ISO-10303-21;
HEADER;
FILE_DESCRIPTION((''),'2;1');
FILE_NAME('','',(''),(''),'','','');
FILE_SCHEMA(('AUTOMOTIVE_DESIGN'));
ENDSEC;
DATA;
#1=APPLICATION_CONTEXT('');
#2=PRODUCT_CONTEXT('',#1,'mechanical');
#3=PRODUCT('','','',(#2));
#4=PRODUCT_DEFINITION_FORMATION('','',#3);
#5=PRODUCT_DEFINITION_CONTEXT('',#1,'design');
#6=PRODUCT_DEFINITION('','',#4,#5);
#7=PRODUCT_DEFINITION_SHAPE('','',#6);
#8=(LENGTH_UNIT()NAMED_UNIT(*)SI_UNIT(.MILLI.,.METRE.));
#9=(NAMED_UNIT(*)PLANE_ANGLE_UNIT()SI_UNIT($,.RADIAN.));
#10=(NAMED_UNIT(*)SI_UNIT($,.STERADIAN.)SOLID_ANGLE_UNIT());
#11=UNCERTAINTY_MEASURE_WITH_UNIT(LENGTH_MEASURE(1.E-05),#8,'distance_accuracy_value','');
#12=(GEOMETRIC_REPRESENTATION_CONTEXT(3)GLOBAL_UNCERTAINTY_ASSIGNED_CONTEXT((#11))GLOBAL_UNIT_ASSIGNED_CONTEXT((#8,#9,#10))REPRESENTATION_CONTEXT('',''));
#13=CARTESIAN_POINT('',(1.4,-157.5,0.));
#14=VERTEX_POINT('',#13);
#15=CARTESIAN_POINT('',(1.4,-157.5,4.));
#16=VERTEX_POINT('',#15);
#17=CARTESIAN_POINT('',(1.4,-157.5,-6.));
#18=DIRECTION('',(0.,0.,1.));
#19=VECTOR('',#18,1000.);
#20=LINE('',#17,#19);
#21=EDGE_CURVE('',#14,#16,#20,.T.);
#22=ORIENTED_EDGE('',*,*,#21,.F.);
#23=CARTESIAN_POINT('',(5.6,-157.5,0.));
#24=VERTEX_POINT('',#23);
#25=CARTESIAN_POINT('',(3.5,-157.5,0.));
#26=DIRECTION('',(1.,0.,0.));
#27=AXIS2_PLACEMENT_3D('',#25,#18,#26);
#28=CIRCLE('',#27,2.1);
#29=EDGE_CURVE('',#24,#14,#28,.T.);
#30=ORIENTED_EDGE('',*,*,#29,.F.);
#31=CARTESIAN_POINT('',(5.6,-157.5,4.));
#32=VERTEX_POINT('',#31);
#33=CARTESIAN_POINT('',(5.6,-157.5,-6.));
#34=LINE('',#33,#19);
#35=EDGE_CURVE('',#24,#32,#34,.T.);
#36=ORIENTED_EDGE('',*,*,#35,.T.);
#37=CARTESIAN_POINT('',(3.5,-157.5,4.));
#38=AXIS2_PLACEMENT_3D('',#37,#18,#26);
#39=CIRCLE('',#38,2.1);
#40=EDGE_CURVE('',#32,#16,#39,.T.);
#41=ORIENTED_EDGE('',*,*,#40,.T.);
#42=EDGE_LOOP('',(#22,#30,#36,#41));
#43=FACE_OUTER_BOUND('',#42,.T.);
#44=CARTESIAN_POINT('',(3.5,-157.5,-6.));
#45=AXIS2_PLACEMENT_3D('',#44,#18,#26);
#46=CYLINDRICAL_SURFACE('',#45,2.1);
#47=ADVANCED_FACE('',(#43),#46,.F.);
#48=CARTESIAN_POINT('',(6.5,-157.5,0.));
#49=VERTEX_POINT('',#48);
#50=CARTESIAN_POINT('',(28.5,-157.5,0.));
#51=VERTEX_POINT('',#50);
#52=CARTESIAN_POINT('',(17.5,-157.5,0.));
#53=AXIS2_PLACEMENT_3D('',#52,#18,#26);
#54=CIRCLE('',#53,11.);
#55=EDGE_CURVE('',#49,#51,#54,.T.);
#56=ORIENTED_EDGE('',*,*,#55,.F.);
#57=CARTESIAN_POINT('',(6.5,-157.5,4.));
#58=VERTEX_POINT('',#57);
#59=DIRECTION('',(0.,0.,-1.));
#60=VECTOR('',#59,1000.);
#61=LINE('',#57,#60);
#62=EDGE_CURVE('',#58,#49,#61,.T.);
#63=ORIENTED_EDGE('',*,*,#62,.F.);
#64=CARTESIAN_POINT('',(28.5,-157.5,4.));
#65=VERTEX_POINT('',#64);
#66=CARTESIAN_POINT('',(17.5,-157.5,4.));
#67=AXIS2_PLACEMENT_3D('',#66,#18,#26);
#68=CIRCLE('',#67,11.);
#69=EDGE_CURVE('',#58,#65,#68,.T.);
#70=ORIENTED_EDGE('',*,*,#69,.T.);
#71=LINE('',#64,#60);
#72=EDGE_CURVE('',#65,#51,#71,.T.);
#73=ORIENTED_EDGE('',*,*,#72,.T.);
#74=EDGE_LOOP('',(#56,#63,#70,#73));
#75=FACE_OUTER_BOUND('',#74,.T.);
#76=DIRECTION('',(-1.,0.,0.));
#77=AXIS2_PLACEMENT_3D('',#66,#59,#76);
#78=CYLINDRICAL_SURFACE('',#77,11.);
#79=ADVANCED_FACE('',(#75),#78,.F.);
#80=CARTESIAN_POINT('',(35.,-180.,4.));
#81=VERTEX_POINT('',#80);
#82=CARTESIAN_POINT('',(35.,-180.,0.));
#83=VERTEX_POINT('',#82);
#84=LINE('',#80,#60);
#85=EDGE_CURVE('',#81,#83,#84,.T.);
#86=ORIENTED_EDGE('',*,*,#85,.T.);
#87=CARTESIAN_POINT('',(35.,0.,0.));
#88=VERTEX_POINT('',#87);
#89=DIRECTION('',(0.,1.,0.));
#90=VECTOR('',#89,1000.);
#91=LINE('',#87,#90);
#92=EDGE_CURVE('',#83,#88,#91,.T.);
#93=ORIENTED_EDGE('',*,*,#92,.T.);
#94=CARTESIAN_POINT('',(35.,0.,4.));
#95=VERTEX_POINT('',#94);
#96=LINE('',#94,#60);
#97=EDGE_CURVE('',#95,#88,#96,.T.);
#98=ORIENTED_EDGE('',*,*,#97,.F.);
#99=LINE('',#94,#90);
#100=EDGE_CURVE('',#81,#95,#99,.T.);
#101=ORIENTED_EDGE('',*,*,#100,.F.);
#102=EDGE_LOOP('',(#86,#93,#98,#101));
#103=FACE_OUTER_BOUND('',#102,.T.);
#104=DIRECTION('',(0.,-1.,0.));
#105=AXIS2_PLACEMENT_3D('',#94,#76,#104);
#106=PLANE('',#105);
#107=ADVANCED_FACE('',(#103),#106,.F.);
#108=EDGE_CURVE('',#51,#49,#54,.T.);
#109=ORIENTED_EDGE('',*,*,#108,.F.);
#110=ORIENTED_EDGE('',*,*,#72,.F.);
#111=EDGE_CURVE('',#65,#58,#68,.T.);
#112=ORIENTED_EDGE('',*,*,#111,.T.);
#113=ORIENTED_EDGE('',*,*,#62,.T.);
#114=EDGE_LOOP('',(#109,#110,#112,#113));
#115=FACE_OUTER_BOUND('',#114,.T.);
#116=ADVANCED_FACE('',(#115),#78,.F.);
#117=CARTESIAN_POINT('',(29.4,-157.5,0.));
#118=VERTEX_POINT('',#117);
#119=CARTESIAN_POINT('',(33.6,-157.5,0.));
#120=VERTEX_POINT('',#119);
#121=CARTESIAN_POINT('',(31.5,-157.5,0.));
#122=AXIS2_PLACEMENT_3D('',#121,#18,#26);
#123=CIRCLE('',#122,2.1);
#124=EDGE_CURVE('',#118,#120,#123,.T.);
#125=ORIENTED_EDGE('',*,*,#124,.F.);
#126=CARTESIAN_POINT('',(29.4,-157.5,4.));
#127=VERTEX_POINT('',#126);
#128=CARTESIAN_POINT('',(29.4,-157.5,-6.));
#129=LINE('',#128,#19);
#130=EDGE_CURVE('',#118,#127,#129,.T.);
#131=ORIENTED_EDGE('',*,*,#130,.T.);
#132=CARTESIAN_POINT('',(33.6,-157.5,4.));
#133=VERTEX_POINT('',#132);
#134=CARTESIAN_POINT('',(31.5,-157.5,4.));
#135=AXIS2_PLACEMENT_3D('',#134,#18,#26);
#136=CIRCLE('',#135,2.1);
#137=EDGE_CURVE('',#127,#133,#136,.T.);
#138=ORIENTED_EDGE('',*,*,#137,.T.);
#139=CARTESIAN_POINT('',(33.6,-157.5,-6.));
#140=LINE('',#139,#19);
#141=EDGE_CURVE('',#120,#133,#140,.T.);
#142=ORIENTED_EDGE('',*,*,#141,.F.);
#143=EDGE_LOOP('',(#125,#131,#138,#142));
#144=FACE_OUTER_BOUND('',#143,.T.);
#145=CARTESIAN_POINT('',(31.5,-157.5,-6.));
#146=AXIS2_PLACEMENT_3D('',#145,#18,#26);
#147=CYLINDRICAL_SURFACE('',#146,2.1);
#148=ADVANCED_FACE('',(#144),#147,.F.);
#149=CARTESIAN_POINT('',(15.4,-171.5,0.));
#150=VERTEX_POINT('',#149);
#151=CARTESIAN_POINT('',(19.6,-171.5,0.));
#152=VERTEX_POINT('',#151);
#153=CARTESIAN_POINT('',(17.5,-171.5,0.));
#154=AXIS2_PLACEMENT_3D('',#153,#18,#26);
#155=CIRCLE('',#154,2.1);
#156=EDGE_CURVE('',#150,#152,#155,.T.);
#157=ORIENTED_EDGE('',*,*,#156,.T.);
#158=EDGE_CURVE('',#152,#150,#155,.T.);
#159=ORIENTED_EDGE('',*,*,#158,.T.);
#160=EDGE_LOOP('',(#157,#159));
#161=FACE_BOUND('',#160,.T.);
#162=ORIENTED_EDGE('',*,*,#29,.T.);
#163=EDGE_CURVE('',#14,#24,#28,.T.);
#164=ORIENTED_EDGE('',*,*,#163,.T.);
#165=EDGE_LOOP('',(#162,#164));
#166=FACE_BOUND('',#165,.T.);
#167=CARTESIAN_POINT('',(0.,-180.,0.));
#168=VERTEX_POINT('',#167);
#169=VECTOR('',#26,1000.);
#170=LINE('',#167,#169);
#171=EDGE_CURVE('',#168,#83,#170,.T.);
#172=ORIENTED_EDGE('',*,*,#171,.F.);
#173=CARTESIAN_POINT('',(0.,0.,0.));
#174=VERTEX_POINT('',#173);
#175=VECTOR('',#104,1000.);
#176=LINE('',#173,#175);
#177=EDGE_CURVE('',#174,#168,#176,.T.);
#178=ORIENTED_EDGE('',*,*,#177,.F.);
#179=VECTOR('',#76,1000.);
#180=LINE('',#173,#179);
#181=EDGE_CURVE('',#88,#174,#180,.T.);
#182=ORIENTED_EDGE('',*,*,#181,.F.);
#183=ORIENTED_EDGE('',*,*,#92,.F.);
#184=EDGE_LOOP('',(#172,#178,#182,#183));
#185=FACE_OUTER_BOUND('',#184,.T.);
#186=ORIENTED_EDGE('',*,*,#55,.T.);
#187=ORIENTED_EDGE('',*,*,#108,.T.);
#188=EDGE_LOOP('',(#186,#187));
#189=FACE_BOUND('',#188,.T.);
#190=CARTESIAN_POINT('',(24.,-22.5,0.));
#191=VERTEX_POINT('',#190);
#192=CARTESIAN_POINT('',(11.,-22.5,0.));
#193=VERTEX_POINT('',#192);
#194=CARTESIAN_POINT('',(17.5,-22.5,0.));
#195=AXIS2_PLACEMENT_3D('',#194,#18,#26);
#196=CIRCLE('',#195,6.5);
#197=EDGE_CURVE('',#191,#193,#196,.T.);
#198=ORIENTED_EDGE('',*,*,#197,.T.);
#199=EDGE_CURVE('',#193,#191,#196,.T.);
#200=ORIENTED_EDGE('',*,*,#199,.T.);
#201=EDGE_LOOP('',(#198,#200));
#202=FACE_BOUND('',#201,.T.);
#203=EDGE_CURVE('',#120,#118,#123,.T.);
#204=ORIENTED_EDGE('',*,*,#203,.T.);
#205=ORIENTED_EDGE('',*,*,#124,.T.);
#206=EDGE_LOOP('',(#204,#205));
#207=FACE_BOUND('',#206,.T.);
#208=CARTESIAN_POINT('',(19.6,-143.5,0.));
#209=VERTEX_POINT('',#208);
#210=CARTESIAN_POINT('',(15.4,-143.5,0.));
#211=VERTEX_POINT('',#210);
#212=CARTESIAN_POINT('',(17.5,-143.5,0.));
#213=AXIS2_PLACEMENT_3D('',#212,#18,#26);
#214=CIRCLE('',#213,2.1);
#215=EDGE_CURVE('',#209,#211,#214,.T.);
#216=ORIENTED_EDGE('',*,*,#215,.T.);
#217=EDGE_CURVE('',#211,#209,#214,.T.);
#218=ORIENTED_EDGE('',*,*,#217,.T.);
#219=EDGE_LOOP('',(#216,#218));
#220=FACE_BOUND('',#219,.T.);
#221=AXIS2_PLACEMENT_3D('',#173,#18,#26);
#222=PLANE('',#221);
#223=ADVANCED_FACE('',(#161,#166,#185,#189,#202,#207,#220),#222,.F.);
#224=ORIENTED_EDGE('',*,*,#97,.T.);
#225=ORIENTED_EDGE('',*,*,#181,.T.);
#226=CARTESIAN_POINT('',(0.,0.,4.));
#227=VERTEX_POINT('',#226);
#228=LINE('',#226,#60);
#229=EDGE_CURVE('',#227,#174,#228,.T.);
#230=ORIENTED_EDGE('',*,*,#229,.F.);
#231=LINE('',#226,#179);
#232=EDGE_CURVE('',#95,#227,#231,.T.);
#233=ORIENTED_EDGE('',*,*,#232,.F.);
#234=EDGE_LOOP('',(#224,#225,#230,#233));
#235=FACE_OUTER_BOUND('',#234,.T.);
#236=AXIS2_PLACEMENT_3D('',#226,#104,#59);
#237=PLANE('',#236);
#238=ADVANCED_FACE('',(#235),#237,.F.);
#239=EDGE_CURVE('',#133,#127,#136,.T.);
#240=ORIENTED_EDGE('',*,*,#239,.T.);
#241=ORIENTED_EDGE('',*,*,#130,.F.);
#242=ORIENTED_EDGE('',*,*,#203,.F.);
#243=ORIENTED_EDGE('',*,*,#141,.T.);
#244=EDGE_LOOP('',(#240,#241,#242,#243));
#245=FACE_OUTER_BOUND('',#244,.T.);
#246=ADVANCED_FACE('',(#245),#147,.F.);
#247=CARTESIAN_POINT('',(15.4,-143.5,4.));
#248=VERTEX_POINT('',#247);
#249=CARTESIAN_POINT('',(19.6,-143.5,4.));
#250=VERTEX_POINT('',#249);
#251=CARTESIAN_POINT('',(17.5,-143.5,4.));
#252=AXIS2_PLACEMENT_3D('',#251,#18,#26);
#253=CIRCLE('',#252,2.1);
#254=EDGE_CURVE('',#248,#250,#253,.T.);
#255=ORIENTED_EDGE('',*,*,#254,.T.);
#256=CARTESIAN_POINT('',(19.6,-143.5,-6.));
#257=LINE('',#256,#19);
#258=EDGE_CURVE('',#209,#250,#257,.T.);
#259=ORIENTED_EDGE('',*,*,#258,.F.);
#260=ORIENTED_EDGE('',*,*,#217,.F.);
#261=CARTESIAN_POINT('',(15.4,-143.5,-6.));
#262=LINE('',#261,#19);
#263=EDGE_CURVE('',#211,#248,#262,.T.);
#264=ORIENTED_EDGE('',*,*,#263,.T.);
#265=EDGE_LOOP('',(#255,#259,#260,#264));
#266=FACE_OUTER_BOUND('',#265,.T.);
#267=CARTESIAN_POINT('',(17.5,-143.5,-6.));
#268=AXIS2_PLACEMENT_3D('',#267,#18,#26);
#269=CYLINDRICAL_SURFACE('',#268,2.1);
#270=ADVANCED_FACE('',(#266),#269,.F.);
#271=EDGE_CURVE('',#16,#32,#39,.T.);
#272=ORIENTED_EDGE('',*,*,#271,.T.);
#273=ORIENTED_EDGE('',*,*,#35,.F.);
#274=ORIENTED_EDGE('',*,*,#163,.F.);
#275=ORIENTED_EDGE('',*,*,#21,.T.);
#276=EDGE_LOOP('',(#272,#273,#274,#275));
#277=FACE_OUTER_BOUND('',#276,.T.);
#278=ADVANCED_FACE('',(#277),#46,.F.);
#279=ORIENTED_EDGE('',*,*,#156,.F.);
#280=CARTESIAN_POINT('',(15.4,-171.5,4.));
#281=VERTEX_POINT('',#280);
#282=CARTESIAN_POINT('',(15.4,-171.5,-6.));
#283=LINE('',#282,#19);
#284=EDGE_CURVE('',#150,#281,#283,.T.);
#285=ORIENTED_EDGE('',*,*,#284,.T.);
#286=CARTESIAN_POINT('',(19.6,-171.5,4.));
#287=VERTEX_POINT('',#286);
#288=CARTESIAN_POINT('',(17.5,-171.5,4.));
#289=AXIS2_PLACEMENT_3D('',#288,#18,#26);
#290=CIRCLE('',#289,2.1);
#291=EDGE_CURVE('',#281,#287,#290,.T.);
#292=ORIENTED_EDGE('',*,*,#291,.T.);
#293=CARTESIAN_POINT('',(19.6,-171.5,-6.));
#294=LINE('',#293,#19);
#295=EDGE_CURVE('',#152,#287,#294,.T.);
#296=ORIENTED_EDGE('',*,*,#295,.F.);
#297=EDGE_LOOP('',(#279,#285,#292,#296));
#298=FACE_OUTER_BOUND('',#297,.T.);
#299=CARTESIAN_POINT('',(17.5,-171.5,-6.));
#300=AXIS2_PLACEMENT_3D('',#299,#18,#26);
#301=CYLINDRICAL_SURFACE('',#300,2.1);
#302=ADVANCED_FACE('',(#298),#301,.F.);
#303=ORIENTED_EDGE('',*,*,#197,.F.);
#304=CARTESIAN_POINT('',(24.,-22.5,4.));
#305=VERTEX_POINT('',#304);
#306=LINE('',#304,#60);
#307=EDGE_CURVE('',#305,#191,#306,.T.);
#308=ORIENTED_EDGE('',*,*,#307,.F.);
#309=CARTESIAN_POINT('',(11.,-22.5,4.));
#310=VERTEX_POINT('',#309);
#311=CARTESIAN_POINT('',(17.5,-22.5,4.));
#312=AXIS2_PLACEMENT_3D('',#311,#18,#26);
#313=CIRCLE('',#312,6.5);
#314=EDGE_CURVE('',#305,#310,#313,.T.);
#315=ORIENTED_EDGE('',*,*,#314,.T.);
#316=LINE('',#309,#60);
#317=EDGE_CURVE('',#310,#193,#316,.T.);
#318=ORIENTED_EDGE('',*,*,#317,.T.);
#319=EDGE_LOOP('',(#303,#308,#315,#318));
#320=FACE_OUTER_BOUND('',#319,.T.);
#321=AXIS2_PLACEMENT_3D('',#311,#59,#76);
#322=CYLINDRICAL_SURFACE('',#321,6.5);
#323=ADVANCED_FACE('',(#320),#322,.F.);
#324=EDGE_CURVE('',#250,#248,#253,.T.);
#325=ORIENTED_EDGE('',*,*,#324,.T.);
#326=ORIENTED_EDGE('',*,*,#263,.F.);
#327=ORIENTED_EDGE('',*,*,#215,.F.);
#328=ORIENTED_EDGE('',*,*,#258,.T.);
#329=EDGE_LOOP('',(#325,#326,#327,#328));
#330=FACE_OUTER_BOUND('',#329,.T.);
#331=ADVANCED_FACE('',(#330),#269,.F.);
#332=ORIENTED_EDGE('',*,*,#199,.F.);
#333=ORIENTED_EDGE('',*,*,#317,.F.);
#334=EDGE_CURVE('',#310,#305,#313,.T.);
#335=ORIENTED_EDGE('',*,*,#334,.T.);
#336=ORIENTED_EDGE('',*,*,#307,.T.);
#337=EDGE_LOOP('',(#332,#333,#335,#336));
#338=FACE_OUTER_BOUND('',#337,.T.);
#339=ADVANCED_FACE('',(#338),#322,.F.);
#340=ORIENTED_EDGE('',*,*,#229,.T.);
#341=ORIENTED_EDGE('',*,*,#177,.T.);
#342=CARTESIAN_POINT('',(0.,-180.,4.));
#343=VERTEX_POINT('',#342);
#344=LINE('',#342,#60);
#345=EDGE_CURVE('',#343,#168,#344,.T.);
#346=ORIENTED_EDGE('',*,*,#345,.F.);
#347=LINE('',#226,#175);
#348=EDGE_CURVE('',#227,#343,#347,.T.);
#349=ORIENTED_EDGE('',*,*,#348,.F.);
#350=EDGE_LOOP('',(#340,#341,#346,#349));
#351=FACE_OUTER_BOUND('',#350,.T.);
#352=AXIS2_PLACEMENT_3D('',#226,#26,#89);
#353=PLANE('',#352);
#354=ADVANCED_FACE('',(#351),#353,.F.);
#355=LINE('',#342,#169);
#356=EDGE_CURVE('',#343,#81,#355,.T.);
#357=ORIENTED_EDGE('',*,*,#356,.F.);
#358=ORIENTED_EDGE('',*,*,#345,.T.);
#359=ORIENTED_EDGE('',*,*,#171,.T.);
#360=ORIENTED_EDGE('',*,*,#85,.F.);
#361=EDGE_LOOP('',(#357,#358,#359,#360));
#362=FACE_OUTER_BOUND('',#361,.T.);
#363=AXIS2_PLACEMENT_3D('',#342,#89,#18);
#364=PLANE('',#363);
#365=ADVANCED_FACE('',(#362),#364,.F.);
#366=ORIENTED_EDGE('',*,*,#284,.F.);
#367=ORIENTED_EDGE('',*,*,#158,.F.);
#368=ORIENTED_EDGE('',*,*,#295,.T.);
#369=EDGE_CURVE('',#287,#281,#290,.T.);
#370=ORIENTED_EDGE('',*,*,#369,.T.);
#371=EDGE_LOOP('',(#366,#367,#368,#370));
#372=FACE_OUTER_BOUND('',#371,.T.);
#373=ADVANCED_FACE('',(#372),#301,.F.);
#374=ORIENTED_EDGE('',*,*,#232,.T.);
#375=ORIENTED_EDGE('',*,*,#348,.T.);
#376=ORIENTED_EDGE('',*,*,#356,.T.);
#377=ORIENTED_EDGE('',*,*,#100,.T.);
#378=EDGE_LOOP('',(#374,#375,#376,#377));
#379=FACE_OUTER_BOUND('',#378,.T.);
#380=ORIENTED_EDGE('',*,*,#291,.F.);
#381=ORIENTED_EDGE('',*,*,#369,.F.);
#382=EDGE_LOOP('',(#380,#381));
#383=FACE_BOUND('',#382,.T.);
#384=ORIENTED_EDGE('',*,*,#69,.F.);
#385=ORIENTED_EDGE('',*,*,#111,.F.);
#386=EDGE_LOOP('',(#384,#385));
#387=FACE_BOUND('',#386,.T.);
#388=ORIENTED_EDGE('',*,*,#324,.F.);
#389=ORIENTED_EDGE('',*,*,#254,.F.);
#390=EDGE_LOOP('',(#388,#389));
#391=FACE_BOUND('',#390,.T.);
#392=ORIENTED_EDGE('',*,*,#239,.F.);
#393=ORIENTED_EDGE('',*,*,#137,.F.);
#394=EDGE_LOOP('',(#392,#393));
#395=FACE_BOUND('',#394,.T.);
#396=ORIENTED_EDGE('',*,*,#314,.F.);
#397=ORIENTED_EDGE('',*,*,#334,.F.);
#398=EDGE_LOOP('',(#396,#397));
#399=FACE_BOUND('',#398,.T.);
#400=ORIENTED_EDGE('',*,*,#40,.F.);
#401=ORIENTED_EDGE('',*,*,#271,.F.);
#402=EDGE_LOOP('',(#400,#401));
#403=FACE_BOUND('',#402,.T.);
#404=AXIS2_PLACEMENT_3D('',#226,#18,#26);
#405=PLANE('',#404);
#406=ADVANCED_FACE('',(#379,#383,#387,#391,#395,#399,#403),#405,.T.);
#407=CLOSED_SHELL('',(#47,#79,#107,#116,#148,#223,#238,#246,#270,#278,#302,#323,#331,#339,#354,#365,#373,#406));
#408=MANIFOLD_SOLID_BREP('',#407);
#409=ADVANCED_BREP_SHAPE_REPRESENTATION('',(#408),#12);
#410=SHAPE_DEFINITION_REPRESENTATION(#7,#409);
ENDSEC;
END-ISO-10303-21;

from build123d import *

# Parameters (mm, degrees)
SKETCH1_W           = 35
SKETCH1_H           = 180
SKETCH1_R           = 6.5
SKETCH1_R_2         = 11
BOSS_EXTRUDE1_DEPTH = 4
SKETCH2_R           = 2.1
CUT_EXTRUDE2_DEPTH  = 10


with BuildPart() as part:
    # Sketch1 → Boss-Extrude1 (new body)
    with BuildSketch(Plane.XY):
        with Locations((17.5, -90)):
            Rectangle(SKETCH1_W, SKETCH1_H)
        with Locations((17.5, -22.5)):
            Circle(SKETCH1_R, mode=Mode.SUBTRACT)
        with Locations((17.5, -157.5)):
            Circle(SKETCH1_R_2, mode=Mode.SUBTRACT)
    extrude(amount=BOSS_EXTRUDE1_DEPTH)

    # Sketch2 → Cut-Extrude2 (cut)
    with BuildSketch(Plane.XY.offset(4)):
        with Locations((3.5, -157.5)):
            Circle(SKETCH2_R)
        with Locations((17.5, -143.5)):
            Circle(SKETCH2_R)
        with Locations((31.5, -157.5)):
            Circle(SKETCH2_R)
        with Locations((17.5, -171.5)):
            Circle(SKETCH2_R)
    extrude(amount=-CUT_EXTRUDE2_DEPTH, mode=Mode.SUBTRACT)


solid = part.part
